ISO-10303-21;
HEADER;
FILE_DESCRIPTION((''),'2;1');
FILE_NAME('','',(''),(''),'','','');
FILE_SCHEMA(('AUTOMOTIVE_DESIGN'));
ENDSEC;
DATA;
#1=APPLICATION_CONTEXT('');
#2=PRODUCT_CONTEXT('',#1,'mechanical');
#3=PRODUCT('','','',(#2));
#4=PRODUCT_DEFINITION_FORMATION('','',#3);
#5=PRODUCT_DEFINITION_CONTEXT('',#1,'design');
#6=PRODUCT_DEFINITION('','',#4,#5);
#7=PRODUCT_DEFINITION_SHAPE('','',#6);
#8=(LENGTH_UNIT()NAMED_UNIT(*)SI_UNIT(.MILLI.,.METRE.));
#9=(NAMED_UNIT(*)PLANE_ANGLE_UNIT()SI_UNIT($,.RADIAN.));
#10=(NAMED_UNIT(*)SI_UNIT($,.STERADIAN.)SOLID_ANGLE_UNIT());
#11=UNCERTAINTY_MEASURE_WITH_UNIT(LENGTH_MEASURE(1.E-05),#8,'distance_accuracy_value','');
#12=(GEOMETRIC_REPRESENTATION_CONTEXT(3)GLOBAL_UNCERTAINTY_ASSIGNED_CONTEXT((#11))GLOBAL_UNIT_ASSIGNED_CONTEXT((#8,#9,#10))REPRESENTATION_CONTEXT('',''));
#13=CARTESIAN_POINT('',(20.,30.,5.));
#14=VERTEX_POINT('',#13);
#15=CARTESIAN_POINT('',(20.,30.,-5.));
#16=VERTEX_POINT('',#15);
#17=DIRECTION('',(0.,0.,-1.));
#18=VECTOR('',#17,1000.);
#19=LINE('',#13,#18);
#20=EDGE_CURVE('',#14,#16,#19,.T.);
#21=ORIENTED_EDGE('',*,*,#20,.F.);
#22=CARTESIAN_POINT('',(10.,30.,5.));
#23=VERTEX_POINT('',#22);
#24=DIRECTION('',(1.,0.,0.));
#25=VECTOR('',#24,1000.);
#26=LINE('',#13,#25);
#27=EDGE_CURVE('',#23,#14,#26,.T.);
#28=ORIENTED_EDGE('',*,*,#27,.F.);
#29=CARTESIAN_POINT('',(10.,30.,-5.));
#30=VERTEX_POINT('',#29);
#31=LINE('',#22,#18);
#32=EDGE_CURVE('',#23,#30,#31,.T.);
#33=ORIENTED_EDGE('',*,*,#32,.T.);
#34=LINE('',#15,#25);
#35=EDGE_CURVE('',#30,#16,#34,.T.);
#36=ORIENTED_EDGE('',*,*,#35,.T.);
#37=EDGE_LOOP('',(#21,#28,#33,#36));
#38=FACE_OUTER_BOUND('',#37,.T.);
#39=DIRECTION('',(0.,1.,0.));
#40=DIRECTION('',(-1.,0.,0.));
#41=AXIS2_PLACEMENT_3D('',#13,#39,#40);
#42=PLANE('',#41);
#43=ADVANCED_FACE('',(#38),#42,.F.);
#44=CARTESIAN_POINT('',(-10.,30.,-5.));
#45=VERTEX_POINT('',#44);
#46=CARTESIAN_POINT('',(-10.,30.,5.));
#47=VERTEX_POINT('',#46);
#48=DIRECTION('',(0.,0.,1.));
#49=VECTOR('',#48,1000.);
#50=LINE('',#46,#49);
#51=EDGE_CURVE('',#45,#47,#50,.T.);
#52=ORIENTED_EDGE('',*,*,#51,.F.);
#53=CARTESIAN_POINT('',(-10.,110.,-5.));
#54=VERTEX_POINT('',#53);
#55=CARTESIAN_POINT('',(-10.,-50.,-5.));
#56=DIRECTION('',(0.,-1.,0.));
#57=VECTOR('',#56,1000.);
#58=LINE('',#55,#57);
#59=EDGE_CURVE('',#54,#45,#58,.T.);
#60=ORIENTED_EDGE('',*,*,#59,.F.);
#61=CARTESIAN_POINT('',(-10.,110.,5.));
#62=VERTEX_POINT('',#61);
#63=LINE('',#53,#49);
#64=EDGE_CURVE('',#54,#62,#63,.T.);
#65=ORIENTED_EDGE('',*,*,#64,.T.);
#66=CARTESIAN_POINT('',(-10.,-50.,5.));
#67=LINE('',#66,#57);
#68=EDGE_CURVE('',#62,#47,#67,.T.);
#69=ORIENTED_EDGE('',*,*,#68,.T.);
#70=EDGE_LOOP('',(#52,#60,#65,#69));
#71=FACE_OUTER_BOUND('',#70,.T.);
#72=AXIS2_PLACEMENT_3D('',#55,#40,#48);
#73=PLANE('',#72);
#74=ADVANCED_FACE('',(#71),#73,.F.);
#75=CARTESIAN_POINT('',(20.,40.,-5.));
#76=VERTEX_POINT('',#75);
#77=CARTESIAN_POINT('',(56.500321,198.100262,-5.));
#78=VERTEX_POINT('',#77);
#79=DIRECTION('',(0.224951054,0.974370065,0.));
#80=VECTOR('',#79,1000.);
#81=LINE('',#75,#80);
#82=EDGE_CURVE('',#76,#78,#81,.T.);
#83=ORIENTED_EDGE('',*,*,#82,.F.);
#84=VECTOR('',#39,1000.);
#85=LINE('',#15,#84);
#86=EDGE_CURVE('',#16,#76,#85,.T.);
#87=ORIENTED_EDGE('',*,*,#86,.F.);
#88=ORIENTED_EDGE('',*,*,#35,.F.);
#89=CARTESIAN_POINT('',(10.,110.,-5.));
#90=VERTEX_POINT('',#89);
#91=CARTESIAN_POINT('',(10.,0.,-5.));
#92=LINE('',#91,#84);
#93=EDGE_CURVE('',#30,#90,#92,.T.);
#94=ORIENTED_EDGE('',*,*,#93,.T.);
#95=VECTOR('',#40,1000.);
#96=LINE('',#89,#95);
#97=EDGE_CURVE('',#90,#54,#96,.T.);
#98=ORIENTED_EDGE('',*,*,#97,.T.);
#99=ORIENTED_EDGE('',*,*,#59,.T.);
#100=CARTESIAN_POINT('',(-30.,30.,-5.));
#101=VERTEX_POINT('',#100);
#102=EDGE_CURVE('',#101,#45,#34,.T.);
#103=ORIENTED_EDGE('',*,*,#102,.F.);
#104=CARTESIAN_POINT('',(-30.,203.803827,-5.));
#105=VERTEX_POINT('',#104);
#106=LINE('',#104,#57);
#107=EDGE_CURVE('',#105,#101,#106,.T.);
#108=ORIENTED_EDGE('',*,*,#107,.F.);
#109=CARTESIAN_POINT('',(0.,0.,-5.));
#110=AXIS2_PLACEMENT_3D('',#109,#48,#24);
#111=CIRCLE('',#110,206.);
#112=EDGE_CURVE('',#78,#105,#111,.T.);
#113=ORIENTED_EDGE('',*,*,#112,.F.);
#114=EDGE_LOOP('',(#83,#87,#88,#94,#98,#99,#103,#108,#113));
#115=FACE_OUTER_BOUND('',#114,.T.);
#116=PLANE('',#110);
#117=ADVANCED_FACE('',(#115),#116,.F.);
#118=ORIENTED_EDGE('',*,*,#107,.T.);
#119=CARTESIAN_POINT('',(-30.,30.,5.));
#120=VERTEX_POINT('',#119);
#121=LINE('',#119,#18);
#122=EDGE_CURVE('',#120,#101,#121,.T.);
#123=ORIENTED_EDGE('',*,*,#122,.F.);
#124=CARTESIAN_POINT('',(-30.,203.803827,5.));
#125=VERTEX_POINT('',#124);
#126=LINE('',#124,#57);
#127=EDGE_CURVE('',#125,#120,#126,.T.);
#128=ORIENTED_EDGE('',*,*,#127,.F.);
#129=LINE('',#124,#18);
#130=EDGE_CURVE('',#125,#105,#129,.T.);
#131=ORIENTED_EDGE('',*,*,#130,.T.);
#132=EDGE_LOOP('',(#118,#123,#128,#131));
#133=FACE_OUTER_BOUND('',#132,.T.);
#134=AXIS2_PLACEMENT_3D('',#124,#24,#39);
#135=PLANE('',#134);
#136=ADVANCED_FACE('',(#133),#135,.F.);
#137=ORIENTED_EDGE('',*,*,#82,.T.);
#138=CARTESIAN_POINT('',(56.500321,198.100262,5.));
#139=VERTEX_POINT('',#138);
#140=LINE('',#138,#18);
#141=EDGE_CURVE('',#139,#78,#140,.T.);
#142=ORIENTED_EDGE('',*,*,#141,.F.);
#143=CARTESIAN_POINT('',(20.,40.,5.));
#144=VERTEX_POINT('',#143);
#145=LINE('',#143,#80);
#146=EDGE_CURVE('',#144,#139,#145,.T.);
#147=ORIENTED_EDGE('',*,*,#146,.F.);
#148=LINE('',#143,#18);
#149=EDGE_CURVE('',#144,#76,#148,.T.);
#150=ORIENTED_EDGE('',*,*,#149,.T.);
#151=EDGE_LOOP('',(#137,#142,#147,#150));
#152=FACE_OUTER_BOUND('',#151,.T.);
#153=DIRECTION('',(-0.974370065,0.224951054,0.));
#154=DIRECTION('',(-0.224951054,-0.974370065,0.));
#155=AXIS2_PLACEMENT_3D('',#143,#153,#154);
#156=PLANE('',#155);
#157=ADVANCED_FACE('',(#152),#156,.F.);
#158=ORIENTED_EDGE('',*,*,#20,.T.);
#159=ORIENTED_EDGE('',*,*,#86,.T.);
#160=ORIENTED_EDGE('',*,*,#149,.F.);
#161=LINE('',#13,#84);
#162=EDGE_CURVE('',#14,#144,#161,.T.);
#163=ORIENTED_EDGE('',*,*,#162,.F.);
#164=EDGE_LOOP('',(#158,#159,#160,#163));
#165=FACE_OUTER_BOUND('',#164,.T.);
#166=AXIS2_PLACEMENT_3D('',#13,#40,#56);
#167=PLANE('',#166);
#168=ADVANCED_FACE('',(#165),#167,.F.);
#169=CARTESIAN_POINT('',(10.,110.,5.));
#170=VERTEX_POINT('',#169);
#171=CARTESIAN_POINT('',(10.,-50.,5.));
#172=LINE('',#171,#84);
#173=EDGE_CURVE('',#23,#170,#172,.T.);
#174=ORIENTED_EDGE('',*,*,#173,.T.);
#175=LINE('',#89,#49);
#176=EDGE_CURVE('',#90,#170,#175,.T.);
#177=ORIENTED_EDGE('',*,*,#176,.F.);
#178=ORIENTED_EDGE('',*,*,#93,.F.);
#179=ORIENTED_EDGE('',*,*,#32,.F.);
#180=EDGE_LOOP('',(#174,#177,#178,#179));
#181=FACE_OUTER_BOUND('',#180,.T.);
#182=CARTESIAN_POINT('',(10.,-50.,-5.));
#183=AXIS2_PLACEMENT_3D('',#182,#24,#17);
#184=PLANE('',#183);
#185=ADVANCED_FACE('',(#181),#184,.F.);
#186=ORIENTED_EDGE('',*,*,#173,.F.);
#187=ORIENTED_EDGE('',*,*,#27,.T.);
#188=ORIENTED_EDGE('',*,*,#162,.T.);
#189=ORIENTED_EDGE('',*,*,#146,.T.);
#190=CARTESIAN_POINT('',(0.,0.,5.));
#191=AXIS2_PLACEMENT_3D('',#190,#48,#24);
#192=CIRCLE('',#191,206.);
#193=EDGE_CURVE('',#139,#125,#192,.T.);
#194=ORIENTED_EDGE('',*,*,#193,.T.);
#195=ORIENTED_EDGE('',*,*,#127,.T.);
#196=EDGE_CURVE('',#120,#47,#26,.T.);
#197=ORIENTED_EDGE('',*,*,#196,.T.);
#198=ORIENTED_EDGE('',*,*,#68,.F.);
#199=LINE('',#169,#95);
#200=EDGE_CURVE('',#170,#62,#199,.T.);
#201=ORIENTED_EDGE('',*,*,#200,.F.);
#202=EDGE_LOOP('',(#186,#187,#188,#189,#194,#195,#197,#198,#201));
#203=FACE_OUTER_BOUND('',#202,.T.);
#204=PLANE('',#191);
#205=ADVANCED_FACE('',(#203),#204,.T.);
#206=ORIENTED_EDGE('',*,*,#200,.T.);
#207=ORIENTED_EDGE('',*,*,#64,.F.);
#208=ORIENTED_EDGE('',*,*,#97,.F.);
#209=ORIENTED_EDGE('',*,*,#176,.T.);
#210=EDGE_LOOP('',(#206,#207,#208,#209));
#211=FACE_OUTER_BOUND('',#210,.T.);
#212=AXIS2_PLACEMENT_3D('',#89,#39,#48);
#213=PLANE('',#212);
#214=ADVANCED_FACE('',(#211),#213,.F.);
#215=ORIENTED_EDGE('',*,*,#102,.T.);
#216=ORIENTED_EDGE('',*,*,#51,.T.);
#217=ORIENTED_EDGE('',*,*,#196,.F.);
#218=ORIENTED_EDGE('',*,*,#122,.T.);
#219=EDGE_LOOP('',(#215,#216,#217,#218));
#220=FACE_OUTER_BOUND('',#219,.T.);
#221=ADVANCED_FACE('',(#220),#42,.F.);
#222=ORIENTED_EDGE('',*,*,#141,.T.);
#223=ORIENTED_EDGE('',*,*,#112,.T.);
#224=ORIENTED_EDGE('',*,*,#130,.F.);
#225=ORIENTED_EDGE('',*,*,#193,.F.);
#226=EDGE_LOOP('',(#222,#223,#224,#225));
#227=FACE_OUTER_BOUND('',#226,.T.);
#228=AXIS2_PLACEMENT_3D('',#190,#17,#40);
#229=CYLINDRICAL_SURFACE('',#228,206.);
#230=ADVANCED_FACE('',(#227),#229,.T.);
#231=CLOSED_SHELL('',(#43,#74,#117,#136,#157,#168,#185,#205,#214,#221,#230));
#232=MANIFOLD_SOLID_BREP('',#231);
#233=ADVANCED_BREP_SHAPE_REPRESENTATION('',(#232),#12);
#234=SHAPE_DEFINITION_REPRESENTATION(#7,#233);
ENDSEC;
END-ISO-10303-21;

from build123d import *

# Parameters (mm, degrees)
BOSS_EXTRUDE1_DEPTH = 5
SKETCH2_W           = 20
SKETCH2_H           = 160
CUT_EXTRUDE1_DEPTH  = 10


with BuildPart() as part:
    # Sketch1 → Boss-Extrude1 (new, symmetric)
    with BuildSketch(Plane.XY):
        with BuildLine():
            Line((-30, 203.803827246), (-30, 30))
            Line((-30, 30), (20, 30))
            Line((20, 30), (20, 40))
            Line((20, 40), (56.500321431, 198.100261681))
            ThreePointArc((56.500321431, 198.100261681), (13.55357606, 205.553644035), (-30, 203.803827246))
        make_face()
    extrude(amount=BOSS_EXTRUDE1_DEPTH, both=True)

    # Sketch2 → Cut-Extrude1 (cut)
    with BuildSketch(Plane.XY.offset(5)):
        with Locations((0, 30)):
            Rectangle(SKETCH2_W, SKETCH2_H)
    extrude(amount=-CUT_EXTRUDE1_DEPTH, mode=Mode.SUBTRACT)


solid = part.part
